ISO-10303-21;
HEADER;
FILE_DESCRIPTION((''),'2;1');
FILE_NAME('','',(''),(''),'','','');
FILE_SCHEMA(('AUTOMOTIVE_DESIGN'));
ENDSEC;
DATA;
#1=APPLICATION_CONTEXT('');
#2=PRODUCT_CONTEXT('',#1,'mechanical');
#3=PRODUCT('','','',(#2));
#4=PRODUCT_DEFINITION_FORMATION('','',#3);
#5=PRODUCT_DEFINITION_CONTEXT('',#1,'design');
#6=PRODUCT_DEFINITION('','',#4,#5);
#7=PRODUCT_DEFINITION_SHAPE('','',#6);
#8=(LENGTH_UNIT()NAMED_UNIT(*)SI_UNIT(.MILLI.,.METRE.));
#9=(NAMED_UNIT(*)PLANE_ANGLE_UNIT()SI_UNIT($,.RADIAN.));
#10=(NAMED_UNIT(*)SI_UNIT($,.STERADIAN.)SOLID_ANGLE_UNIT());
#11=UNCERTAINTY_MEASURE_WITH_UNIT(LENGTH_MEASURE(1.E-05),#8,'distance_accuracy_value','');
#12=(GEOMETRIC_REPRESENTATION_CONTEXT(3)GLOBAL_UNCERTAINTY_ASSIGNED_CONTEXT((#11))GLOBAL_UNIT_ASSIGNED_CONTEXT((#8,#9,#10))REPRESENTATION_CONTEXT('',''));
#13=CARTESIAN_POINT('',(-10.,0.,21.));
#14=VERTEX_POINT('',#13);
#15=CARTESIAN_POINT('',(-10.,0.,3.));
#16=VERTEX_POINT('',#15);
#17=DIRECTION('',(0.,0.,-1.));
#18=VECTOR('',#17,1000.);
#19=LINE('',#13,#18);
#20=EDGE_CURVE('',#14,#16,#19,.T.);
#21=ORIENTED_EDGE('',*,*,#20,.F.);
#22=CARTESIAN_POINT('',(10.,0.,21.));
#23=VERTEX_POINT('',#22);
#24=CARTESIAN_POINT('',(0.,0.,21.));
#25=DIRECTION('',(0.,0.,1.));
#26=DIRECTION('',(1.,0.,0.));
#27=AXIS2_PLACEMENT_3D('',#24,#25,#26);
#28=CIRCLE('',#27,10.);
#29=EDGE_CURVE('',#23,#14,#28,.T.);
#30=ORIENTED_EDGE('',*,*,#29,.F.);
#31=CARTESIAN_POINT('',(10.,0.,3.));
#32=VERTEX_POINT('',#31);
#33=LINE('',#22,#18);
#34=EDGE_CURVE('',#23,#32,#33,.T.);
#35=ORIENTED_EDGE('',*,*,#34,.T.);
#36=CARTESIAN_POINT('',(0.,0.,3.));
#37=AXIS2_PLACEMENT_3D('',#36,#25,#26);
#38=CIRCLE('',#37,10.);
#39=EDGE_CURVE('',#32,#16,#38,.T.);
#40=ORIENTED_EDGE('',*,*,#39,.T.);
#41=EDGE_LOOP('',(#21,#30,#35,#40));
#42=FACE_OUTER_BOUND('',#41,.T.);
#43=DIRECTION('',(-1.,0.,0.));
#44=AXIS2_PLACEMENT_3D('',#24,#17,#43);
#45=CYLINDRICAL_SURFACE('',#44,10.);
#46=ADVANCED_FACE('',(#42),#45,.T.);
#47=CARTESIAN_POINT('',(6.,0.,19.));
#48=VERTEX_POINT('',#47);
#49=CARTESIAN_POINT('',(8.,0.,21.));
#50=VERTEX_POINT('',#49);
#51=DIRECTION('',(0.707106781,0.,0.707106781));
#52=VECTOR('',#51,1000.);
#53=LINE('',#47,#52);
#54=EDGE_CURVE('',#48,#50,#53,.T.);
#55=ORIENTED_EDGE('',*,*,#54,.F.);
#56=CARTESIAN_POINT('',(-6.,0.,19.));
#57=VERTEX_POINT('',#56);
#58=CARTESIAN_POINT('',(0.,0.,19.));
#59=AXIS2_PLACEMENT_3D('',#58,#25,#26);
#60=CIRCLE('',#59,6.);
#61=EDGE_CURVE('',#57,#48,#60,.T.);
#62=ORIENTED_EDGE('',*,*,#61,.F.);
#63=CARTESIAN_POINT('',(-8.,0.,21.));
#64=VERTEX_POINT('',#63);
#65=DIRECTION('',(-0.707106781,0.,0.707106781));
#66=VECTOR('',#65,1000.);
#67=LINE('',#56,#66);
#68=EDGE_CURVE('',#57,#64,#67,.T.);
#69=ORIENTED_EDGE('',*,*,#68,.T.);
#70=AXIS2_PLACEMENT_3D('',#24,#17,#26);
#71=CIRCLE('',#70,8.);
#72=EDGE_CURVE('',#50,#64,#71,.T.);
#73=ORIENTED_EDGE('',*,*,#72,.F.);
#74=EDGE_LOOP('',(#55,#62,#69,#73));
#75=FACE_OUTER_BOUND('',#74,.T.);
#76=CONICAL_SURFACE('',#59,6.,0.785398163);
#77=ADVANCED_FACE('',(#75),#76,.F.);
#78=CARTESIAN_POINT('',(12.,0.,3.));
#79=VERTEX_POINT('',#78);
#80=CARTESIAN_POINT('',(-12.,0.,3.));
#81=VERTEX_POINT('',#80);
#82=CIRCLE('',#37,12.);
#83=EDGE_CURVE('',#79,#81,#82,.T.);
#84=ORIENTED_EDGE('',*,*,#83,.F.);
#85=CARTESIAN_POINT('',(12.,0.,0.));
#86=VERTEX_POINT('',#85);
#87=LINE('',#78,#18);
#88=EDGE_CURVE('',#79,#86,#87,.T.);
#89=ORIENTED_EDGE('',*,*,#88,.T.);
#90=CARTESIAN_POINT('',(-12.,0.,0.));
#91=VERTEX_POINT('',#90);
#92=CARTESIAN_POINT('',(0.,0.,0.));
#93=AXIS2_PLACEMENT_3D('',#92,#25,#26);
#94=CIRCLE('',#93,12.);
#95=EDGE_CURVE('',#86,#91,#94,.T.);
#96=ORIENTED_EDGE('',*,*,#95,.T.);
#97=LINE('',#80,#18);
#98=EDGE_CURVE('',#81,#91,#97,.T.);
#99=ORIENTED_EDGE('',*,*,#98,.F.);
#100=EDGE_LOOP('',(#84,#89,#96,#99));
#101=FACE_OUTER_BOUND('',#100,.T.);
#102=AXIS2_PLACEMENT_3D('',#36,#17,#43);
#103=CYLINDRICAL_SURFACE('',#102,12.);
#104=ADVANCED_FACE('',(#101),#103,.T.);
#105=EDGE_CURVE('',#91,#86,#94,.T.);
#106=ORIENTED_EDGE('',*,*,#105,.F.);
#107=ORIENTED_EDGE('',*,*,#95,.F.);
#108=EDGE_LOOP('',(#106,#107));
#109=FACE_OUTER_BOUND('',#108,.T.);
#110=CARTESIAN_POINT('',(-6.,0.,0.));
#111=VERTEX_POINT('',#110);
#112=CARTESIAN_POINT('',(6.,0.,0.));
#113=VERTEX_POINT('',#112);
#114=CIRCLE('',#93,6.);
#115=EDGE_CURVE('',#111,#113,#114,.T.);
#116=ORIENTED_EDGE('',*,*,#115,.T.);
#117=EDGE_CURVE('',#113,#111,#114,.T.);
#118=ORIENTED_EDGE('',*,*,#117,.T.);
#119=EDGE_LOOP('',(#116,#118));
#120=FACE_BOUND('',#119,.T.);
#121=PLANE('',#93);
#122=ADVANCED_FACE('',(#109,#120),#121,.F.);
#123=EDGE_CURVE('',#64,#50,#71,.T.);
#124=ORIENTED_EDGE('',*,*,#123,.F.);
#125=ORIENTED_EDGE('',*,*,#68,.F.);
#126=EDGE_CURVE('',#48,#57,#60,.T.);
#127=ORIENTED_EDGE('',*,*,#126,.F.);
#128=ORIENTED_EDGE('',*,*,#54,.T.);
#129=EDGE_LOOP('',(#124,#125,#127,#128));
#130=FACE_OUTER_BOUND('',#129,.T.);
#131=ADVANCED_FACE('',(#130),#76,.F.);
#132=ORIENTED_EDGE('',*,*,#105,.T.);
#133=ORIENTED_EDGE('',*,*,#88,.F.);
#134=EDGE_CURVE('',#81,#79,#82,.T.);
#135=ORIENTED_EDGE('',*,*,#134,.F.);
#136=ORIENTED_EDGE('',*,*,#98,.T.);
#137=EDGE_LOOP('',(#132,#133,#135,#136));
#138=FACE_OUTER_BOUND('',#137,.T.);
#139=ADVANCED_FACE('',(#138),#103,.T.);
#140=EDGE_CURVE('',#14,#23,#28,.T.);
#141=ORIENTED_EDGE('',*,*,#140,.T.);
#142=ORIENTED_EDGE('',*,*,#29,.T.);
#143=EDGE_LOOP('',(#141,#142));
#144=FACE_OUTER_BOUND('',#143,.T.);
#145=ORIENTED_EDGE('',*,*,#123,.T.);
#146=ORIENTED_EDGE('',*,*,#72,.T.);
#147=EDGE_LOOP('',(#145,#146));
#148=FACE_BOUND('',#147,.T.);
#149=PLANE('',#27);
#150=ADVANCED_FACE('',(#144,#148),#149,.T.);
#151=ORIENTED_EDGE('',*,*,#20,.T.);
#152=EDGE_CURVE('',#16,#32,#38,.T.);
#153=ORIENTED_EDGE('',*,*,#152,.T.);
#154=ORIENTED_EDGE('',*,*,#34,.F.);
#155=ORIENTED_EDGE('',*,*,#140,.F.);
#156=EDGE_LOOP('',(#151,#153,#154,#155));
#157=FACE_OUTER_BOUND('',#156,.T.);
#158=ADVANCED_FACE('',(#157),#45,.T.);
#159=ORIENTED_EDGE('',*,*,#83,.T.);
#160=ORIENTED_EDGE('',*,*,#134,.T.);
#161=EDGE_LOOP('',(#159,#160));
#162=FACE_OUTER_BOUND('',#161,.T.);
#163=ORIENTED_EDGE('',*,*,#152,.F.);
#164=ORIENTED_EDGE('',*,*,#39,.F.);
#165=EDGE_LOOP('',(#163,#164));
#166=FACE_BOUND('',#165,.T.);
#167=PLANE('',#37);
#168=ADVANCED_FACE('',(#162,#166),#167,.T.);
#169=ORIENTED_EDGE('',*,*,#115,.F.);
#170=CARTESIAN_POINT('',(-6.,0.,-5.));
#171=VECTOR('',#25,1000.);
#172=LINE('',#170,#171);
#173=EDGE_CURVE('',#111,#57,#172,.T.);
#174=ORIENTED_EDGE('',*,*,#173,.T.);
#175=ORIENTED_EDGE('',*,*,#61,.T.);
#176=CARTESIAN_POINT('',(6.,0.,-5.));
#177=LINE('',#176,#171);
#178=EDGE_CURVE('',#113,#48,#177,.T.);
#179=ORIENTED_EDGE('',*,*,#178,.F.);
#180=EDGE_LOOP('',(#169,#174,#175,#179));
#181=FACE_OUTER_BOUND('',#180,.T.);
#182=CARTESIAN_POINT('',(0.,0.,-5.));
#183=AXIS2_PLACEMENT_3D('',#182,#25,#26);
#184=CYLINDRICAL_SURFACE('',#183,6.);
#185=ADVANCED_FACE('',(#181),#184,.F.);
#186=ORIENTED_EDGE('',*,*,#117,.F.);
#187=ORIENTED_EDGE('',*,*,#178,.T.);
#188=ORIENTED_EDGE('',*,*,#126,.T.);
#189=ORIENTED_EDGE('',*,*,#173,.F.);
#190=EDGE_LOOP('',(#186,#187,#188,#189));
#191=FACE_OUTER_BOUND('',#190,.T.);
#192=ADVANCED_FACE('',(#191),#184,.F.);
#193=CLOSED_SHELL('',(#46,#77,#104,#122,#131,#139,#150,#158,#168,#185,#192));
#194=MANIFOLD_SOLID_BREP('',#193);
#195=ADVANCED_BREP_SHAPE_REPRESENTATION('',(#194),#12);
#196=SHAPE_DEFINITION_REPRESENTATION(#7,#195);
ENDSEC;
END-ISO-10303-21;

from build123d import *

# Parameters (mm, degrees)
SKETCH1_R           = 12
BOSS_EXTRUDE1_DEPTH = 3
SKETCH2_R           = 10
BOSS_EXTRUDE2_DEPTH = 18
SKETCH3_R           = 6
CUT_EXTRUDE1_DEPTH  = 26
CHAMFER1_SIZE       = 2


with BuildPart() as part:
    # Sketch1 → Boss-Extrude1 (new body)
    with BuildSketch(Plane.XY):
        Circle(SKETCH1_R)
    extrude(amount=BOSS_EXTRUDE1_DEPTH)

    # Sketch2 → Boss-Extrude2 (add)
    with BuildSketch(Plane.XY.offset(3)):
        Circle(SKETCH2_R)
    extrude(amount=BOSS_EXTRUDE2_DEPTH)

    # Sketch3 → Cut-Extrude1 (cut)
    with BuildSketch(Plane.XY.offset(21)):
        Circle(SKETCH3_R)
    extrude(amount=-CUT_EXTRUDE1_DEPTH, mode=Mode.SUBTRACT)

    # Chamfer1
    chamfer1_edges = [part.edges().sort_by_distance(p)[0] for p in [
        (-6, 0, 21),
    ]]
    chamfer(chamfer1_edges, length=CHAMFER1_SIZE)


solid = part.part
